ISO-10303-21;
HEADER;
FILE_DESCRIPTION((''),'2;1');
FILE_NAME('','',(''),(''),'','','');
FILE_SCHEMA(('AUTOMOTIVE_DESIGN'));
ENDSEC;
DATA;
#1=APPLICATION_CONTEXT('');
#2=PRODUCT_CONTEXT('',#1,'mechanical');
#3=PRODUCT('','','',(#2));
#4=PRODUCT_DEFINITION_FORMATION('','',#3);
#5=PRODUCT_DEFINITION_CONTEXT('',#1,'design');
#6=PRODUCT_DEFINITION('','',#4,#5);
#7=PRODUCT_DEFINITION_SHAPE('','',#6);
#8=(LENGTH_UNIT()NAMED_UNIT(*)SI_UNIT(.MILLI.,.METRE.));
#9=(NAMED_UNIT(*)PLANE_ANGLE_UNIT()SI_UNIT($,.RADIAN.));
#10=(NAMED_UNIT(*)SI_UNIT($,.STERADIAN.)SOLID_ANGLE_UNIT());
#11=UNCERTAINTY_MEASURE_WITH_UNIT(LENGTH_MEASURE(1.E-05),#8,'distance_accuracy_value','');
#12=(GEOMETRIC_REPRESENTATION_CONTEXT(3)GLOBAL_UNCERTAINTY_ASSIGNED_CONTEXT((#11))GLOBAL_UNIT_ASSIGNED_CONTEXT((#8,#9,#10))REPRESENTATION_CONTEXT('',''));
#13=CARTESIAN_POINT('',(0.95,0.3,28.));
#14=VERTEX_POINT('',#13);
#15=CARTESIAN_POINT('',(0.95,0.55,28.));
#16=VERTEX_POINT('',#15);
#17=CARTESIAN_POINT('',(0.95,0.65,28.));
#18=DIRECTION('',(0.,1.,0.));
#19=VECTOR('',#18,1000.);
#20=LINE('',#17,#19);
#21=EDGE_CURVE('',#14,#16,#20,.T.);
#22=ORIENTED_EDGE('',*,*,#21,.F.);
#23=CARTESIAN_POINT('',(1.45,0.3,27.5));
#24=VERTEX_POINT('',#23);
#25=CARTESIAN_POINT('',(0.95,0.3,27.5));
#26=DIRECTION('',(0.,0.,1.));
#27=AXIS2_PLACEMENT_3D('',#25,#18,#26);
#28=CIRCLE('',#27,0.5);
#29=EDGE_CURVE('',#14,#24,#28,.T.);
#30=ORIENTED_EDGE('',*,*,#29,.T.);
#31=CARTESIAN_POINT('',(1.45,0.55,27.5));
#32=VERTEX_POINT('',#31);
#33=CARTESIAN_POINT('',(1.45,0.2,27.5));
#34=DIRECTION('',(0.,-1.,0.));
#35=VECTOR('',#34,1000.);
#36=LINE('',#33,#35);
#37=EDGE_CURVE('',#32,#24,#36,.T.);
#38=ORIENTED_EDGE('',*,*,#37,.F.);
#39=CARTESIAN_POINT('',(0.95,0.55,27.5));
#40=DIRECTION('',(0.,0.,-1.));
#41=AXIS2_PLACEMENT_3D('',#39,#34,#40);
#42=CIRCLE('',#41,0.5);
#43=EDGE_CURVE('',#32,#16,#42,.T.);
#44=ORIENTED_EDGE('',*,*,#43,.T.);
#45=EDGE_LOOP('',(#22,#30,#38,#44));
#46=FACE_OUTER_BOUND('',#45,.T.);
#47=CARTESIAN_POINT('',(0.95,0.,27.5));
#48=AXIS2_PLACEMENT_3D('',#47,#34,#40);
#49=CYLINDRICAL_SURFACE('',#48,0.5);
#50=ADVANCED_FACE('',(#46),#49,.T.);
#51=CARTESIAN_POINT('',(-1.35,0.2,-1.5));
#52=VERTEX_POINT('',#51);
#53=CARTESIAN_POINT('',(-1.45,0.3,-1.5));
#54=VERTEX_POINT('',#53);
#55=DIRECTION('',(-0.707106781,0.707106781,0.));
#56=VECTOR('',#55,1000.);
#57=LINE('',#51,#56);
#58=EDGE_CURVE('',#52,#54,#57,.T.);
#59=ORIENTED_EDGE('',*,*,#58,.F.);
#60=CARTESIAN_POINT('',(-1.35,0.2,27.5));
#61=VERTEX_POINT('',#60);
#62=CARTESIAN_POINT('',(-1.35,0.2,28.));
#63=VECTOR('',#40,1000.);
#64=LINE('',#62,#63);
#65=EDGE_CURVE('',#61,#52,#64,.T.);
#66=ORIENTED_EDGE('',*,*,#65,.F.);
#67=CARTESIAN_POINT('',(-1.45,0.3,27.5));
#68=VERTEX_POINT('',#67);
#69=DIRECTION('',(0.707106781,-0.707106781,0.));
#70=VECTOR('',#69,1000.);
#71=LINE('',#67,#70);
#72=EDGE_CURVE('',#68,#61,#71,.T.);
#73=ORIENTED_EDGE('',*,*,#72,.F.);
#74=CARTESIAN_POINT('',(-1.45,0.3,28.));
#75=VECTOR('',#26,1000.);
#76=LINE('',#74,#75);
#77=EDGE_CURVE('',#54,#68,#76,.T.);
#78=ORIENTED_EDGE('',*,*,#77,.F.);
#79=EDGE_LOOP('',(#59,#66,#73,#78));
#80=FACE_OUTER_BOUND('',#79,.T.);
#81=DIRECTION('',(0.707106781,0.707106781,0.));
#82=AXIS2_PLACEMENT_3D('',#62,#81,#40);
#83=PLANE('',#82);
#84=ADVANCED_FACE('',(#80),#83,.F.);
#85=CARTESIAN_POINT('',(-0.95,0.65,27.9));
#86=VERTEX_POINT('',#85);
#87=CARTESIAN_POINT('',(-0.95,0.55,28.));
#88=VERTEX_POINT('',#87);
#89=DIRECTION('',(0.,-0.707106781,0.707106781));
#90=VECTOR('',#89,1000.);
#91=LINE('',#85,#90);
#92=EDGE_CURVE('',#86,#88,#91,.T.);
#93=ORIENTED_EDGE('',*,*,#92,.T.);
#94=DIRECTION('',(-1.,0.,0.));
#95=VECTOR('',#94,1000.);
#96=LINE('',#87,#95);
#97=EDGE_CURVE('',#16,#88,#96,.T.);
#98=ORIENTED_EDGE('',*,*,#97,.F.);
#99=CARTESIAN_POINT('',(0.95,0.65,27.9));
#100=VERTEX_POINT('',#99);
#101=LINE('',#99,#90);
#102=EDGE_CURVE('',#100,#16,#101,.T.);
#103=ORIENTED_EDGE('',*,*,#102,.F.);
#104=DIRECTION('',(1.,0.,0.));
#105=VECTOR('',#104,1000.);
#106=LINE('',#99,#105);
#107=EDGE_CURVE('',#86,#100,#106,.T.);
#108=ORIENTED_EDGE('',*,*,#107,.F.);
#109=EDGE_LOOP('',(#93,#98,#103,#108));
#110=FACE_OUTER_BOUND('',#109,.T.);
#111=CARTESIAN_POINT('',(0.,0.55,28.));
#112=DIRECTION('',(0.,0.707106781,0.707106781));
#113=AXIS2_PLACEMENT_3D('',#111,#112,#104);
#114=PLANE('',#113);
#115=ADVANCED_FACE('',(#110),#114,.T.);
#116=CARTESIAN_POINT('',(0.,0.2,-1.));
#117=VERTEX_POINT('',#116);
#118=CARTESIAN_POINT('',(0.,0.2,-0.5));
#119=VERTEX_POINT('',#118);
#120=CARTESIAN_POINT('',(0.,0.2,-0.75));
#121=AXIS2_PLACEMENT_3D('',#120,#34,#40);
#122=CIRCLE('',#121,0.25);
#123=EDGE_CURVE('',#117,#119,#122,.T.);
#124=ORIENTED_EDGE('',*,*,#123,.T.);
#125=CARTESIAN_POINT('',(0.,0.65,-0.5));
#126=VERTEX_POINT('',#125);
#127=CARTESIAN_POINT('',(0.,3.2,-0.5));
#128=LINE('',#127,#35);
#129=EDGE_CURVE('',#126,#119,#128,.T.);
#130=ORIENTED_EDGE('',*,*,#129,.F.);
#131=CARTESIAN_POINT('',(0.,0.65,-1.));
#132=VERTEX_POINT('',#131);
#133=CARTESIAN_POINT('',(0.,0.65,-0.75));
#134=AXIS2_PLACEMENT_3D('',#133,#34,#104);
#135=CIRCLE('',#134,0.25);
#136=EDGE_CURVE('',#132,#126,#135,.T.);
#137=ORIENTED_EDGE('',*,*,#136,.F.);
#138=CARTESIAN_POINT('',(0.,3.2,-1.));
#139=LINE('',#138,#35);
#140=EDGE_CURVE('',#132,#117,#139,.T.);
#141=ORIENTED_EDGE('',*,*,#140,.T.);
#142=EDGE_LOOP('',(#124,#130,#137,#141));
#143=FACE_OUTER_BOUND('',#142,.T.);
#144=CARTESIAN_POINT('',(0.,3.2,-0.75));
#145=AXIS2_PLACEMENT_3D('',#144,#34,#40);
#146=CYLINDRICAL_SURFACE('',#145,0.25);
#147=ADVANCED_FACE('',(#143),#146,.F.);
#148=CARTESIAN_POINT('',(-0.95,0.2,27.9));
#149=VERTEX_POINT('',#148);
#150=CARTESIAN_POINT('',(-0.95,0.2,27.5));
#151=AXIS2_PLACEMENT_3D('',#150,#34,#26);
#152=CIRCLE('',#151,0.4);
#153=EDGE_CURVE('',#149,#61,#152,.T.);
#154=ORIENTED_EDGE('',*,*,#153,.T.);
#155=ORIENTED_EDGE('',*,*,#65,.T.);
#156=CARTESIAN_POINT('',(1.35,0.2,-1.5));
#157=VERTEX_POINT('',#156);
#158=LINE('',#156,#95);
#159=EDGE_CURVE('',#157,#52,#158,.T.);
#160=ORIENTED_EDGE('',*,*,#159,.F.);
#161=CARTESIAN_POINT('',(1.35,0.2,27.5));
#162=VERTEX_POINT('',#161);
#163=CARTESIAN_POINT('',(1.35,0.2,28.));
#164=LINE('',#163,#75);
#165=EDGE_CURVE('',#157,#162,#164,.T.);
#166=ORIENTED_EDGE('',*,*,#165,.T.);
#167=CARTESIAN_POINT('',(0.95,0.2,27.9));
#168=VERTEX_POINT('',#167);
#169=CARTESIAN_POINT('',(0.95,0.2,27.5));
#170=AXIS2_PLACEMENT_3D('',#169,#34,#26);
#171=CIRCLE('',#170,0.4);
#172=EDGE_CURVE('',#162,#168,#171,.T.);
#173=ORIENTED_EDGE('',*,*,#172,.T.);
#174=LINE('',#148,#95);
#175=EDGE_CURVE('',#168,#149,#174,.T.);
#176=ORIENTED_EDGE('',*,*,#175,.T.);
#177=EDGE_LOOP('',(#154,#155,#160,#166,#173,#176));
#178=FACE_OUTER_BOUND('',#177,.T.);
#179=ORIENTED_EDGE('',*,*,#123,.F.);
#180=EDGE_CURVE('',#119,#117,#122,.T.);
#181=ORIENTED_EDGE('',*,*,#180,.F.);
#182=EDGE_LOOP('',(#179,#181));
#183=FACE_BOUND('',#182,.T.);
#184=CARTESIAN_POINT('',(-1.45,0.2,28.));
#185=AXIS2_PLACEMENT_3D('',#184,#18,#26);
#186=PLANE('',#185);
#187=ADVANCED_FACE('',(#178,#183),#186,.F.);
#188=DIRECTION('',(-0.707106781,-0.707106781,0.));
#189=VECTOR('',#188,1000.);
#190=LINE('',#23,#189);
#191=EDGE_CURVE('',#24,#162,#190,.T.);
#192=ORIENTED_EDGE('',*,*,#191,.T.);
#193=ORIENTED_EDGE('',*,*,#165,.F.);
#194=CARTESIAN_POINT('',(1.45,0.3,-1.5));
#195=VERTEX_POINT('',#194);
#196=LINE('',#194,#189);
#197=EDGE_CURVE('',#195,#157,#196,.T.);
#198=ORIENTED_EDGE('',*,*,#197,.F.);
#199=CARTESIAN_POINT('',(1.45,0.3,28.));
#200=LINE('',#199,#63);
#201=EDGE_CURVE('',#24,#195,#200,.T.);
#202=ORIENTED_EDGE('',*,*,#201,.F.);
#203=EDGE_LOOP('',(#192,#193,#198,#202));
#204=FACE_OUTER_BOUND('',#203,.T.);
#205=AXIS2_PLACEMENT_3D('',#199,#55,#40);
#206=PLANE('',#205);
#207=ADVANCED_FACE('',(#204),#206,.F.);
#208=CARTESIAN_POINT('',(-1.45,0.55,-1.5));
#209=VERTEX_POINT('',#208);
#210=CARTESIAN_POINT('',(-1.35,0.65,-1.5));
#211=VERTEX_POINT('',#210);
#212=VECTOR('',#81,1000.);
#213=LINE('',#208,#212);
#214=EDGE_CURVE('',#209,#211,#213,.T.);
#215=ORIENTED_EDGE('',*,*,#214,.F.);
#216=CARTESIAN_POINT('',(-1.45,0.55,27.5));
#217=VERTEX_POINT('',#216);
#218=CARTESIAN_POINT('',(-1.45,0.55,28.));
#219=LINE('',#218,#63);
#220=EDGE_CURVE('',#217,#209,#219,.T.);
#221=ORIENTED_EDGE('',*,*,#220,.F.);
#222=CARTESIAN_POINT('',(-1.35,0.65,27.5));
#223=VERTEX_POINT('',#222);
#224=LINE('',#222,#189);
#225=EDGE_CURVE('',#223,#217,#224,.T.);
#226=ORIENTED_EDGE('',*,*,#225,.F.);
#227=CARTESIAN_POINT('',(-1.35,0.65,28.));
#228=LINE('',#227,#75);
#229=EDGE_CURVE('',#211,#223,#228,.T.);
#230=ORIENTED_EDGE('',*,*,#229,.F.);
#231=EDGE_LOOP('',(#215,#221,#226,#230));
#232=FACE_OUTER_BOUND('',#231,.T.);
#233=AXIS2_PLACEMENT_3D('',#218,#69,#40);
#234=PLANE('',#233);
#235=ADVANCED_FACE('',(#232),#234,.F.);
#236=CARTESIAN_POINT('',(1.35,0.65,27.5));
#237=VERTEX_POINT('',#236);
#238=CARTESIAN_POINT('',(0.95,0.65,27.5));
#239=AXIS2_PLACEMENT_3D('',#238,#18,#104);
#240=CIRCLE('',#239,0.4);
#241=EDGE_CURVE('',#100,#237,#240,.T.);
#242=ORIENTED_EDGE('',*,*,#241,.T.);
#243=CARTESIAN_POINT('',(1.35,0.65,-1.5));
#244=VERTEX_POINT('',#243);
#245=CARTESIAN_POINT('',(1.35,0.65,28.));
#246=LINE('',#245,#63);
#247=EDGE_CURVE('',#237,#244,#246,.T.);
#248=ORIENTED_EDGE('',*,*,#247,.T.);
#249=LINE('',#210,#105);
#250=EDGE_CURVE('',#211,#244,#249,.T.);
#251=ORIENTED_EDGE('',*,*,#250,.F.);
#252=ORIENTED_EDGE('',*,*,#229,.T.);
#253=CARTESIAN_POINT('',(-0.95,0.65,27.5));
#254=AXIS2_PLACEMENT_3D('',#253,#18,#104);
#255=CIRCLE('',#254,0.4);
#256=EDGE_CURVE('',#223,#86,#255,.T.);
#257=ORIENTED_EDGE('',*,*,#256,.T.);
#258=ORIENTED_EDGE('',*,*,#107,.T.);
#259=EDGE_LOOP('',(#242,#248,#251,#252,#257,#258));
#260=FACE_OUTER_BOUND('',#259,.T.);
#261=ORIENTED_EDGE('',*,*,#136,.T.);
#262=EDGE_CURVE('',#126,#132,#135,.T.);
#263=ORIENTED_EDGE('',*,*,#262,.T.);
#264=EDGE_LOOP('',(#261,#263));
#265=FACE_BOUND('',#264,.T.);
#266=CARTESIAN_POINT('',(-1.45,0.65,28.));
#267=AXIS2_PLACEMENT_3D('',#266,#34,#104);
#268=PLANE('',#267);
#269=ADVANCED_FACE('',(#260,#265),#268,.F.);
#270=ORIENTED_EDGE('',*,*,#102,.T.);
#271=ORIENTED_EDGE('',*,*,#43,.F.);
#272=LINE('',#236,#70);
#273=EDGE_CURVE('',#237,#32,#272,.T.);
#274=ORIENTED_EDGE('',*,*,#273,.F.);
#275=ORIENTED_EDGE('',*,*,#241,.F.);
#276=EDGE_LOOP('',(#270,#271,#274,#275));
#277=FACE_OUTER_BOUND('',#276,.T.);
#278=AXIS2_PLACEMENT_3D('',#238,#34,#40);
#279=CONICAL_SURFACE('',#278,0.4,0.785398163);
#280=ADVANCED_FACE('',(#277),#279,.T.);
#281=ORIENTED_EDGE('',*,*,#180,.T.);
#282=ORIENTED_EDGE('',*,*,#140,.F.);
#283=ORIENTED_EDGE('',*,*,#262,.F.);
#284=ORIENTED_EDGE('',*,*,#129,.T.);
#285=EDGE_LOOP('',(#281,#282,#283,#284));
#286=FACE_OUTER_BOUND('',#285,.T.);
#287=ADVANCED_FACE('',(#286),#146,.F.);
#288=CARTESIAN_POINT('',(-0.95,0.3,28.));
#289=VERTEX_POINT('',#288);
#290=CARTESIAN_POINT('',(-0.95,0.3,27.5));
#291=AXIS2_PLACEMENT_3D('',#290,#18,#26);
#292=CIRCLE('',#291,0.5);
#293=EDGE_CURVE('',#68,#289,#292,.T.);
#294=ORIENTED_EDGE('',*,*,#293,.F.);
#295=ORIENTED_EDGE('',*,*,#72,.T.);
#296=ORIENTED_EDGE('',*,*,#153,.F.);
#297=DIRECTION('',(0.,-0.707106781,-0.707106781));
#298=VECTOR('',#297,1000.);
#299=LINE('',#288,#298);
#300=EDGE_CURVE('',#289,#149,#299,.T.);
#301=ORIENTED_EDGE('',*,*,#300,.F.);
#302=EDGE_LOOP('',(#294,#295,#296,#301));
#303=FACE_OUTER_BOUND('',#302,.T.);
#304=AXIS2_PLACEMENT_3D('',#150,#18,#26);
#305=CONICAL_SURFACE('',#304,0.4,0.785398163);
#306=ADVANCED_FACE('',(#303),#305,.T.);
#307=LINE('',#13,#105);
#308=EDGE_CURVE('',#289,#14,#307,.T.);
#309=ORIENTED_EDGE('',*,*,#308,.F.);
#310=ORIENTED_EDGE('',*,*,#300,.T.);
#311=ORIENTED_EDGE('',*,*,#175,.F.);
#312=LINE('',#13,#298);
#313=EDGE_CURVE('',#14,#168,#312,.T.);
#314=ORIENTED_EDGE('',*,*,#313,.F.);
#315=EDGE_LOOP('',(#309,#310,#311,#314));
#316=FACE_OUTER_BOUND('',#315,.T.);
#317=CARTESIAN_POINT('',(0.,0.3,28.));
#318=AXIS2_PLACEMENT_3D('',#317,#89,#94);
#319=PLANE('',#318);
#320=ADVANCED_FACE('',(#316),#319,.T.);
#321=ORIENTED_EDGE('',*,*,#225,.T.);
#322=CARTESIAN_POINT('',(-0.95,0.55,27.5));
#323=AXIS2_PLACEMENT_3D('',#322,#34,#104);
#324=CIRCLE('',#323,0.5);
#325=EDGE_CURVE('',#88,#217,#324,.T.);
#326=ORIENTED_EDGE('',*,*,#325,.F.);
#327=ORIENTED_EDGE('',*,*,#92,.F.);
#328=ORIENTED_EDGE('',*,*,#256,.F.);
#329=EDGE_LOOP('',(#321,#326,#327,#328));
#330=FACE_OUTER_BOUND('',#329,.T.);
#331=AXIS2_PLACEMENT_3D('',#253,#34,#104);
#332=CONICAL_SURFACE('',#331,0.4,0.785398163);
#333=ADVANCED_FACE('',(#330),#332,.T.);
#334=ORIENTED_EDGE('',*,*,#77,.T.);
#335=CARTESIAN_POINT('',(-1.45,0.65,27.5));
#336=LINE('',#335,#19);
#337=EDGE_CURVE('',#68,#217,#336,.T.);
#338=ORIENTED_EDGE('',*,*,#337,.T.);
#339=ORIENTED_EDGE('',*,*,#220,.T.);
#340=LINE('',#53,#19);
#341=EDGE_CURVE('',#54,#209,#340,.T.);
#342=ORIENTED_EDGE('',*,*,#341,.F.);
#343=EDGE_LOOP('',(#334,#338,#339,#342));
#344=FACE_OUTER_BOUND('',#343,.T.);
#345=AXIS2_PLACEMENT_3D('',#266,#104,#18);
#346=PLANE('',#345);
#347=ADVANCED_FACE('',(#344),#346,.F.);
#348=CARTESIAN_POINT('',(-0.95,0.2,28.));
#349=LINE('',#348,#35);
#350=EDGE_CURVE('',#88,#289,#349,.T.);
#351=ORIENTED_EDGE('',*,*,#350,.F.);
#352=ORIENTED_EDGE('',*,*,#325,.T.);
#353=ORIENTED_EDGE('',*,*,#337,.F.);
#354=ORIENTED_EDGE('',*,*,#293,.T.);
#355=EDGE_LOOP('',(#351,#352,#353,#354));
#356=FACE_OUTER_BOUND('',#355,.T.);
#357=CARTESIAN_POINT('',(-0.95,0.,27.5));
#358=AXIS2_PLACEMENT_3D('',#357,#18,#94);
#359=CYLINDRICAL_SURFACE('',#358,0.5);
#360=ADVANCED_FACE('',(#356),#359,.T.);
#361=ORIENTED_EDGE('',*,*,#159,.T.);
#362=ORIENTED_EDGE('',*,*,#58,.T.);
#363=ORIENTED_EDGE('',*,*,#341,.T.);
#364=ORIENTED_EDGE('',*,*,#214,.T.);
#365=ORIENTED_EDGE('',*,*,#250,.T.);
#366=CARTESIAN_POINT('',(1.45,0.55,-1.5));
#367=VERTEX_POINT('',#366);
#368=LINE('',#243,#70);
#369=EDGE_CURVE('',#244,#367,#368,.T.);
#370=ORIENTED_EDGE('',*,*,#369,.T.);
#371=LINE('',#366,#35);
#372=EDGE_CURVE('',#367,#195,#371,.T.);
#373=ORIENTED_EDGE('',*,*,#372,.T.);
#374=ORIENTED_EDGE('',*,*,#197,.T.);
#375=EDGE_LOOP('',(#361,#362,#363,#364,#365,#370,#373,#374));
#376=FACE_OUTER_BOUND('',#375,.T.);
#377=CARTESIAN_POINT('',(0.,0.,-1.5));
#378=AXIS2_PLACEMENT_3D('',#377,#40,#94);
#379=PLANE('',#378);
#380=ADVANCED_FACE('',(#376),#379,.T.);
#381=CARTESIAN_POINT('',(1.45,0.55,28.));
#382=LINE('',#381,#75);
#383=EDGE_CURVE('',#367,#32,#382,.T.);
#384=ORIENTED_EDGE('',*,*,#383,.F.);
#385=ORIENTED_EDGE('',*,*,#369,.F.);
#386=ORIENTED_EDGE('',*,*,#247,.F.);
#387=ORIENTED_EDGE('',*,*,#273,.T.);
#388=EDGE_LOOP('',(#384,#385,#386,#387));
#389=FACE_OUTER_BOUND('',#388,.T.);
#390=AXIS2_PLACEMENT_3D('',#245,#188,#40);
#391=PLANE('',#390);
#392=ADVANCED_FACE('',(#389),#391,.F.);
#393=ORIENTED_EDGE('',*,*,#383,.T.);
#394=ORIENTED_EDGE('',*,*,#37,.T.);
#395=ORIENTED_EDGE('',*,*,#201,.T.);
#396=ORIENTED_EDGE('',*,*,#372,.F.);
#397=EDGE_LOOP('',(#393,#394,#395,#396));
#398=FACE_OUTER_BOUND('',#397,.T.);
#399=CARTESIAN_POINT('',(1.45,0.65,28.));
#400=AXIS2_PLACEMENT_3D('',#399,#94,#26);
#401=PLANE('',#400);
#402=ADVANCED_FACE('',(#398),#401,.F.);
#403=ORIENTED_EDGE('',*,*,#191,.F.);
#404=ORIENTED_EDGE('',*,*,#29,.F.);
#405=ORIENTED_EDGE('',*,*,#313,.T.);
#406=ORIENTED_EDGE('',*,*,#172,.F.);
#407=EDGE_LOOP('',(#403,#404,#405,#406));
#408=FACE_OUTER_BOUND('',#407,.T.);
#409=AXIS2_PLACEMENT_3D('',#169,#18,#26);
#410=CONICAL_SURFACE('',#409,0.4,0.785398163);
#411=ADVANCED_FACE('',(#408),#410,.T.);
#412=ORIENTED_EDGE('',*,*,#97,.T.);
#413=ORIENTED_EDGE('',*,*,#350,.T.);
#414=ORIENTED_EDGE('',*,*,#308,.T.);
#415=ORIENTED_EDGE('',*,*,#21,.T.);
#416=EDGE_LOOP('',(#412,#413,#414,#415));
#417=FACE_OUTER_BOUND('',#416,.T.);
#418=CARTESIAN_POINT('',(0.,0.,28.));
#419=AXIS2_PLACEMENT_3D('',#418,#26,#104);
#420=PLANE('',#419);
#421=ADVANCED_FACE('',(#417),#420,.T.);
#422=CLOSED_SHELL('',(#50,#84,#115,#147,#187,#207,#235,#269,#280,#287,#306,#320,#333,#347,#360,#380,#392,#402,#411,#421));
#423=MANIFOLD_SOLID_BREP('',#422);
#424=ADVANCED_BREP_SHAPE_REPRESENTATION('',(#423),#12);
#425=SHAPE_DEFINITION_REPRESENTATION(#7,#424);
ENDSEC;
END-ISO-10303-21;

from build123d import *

# Parameters (mm, degrees)
SKETCH1_W           = 4.5
SKETCH1_H           = 3
BOSS_EXTRUDE1_DEPTH = 8
SKETCH2_W           = 2.9
SKETCH2_H           = 0.45
BOSS_EXTRUDE2_DEPTH = 26.5
FILLET1_R           = 0.5
CHAMFER1_SIZE       = 1
CHAMFER2_SIZE       = 0.1
SKETCH3_R           = 1.525
CUT_EXTRUDE1_DEPTH  = 2.1
SKETCH5_R           = 0.6
CUT_EXTRUDE2_DEPTH  = 2.1
CUT_EXTRUDE3_DEPTH  = 30.466082196
BOSS_EXTRUDE3_DEPTH = 3
SKETCH8_R           = 0.25
CUT_EXTRUDE4_DEPTH  = 3


with BuildPart() as part:
    # Sketch1 → Boss-Extrude1 (new body)
    with BuildSketch(Plane(origin=(0, 0, 0), x_dir=(1, 0, 0), z_dir=(0, 1, 0))):
        Rectangle(SKETCH1_W, SKETCH1_H)
    extrude(amount=BOSS_EXTRUDE1_DEPTH)

    # Sketch2 → Boss-Extrude2 (add)
    with BuildSketch(Plane.XY.offset(1.5)):
        with Locations((0, 0.425)):
            Rectangle(SKETCH2_W, SKETCH2_H)
    extrude(amount=BOSS_EXTRUDE2_DEPTH)

    # Fillet1
    fillet1_edges = [part.edges().sort_by_distance(p)[0] for p in [
        (1.45, 0.425, 28),
        (-1.45, 0.425, 28),
    ]]
    fillet(fillet1_edges, radius=FILLET1_R)

    # Chamfer1
    chamfer1_edges = [part.edges().sort_by_distance(p)[0] for p in [
        (0, 8, 1.5),
    ]]
    chamfer(chamfer1_edges, length=CHAMFER1_SIZE)

    # Chamfer2
    chamfer2_edges = [part.edges().sort_by_distance(p)[0] for p in [
        (0, 0.65, 28),
        (0, 0.2, 28),
        (1.45, 0.2, 14.5),
        (-1.45, 0.2, 14.5),
        (1.303553391, 0.2, 27.853553391),
        (-1.303553391, 0.2, 27.853553391),
        (-1.45, 0.65, 14.5),
        (1.45, 0.65, 14.5),
        (1.303553391, 0.65, 27.853553391),
        (-1.303553391, 0.65, 27.853553391),
    ]]
    chamfer(chamfer2_edges, length=CHAMFER2_SIZE)

    # Sketch3 → Cut-Extrude1 (cut)
    with BuildSketch(Plane.XY.offset(1.5)):
        with Locations((0, 3.825)):
            Circle(SKETCH3_R)
    extrude(amount=-CUT_EXTRUDE1_DEPTH, mode=Mode.SUBTRACT)

    # Sketch5 → Cut-Extrude2 (cut)
    with BuildSketch(Plane.XY.offset(-0.6)):
        with Locations((0, 3.825)):
            Circle(SKETCH5_R)
    extrude(amount=-CUT_EXTRUDE2_DEPTH, mode=Mode.SUBTRACT)

    # Sketch6 → Cut-Extrude3 (cut, through all)
    with BuildSketch(Plane(origin=(2.25, 0, 0), x_dir=(0, 0, -1), z_dir=(1, 0, 0))):
        Polygon((1.5, 8), (-0.5, 8), (-1.5, 7), (-1.5, 0), (1.5, 0), align=None)
    extrude(amount=-CUT_EXTRUDE3_DEPTH, mode=Mode.SUBTRACT)

    # Sketch7 → Boss-Extrude3 (add)
    with BuildSketch(Plane(origin=(0, 0, 1.5), x_dir=(-1, 0, 0), z_dir=(0, 0, -1))):
        Polygon((1.45, 0.55), (1.35, 0.65), (-1.35, 0.65), (-1.45, 0.55), (-1.45, 0.3), (-1.35, 0.2), (1.35, 0.2), (1.45, 0.3), align=None)
    extrude(amount=BOSS_EXTRUDE3_DEPTH)

    # Sketch8 → Cut-Extrude4 (cut)
    with BuildSketch(Plane.XZ.offset(-0.2)):
        with Locations(Location((0, -0.75, 0), (0, 0, 270))):
            Circle(SKETCH8_R)
    extrude(amount=-CUT_EXTRUDE4_DEPTH, mode=Mode.SUBTRACT)


solid = part.part
